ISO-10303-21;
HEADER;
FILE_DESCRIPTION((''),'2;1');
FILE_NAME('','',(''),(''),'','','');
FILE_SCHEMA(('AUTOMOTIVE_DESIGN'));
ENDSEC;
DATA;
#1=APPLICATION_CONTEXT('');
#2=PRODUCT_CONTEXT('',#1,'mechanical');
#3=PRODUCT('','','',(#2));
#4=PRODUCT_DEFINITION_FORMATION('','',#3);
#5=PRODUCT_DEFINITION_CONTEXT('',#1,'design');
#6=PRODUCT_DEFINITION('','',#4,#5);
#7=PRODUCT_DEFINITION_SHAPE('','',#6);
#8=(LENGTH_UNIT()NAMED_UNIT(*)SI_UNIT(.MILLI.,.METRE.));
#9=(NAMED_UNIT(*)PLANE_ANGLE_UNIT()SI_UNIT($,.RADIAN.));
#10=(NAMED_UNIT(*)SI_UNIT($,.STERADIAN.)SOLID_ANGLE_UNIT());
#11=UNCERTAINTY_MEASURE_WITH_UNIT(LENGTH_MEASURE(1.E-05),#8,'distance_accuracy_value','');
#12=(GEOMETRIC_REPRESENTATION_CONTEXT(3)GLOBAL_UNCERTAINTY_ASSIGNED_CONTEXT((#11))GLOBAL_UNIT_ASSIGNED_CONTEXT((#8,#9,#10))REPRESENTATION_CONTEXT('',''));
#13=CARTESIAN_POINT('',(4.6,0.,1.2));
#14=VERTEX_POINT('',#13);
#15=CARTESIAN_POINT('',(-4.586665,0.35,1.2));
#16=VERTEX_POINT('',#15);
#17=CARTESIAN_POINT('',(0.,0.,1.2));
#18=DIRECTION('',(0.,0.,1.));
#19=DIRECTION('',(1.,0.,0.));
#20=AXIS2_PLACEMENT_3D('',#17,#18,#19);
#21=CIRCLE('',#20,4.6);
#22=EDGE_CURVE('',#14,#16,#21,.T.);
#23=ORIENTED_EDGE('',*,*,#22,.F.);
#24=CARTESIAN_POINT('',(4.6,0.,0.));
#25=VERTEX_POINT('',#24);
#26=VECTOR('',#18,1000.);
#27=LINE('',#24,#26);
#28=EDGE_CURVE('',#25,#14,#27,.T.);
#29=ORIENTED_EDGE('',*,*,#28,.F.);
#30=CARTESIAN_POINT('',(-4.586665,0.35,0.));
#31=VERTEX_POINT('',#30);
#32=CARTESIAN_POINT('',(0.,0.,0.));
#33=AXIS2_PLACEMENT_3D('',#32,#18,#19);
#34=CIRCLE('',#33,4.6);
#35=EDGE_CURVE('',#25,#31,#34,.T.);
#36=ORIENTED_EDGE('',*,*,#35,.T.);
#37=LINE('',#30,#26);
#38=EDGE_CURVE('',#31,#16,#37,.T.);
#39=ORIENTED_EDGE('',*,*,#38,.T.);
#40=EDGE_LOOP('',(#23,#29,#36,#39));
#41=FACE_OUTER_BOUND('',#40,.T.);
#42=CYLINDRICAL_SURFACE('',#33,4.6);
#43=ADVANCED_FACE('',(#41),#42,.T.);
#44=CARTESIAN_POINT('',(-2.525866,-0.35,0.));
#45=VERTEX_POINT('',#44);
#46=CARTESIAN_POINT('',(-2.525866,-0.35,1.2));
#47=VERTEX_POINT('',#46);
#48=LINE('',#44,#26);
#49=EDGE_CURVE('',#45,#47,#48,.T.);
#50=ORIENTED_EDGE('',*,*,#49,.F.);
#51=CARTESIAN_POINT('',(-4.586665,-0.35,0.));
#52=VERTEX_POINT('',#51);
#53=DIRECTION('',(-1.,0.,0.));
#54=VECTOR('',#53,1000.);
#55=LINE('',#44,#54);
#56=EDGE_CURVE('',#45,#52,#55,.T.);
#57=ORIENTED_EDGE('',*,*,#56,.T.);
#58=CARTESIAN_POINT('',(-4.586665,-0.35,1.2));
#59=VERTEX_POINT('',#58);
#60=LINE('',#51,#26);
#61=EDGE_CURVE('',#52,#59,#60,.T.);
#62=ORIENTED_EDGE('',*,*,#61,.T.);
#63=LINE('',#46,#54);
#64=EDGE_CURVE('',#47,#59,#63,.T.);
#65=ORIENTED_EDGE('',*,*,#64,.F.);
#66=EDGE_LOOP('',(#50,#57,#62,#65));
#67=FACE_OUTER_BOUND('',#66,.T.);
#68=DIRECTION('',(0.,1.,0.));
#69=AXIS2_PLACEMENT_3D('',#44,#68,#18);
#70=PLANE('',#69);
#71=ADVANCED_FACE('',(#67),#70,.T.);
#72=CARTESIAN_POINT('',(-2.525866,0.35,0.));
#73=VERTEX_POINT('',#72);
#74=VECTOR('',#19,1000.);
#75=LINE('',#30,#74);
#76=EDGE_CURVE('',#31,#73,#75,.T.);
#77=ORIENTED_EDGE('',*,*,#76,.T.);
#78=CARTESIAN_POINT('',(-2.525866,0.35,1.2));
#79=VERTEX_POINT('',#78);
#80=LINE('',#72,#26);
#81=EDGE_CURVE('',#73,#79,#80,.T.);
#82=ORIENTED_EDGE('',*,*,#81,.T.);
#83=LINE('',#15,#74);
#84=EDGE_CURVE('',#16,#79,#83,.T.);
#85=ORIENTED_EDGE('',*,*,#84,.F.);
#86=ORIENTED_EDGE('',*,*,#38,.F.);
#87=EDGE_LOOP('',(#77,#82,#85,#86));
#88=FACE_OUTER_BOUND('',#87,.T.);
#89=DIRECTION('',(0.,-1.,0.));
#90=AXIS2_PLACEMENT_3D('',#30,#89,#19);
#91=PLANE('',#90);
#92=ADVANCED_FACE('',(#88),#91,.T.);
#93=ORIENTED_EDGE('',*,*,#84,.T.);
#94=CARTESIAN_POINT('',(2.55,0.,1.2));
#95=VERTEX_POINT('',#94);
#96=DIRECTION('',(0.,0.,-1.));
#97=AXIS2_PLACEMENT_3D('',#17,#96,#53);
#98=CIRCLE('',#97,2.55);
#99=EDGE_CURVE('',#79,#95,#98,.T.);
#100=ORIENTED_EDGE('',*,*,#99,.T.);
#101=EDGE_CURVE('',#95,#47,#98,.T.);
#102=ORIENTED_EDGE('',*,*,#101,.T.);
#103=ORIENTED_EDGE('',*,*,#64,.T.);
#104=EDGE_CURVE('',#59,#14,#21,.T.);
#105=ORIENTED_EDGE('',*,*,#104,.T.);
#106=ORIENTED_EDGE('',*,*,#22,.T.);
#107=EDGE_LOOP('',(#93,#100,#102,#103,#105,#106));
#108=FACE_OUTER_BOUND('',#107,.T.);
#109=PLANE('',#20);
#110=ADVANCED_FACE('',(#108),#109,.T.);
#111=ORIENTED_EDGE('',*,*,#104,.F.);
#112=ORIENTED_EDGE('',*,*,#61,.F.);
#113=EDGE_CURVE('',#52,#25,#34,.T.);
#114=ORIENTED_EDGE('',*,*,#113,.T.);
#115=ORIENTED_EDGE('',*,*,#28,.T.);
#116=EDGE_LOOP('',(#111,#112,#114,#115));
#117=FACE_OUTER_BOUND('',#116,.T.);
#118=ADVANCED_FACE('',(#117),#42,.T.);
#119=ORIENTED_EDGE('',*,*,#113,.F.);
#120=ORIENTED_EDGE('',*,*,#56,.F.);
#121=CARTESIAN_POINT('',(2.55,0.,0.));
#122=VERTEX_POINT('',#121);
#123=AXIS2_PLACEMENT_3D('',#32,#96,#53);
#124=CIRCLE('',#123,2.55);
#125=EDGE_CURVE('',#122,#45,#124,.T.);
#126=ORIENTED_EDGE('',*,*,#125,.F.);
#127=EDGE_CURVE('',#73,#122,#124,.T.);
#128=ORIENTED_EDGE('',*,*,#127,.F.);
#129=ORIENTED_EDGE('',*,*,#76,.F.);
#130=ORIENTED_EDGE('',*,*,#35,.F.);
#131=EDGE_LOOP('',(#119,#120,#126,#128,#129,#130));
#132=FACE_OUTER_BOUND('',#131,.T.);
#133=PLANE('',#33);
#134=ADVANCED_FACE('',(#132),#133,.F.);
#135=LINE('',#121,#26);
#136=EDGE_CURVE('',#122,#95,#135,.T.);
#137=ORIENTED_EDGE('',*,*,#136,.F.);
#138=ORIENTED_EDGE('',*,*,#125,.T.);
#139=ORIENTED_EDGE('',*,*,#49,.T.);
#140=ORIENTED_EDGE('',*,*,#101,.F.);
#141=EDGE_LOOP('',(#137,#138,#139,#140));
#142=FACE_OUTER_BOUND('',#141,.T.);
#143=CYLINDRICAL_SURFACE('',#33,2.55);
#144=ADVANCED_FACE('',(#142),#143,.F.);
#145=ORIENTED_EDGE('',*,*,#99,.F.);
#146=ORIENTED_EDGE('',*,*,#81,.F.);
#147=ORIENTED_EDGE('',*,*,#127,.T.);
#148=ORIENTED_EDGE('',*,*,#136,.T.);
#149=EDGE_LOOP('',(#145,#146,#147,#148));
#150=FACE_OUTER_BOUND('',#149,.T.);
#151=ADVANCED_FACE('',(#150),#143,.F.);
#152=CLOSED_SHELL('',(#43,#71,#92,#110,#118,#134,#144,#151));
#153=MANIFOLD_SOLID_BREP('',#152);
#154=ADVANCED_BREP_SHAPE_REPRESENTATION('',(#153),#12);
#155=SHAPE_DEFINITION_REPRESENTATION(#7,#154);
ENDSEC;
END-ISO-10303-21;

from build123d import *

# Parameters (mm, degrees)
EXTRUDE_1_DEPTH = 1.2


with BuildPart() as part:
    # 草图1 → 凸台-拉伸1 (new body)
    with BuildSketch(Plane.XY.offset(1.2)):
        with BuildLine():
            Line((-4.586665455, 0.35), (-2.525866188, 0.35))
            ThreePointArc((-2.525866188, 0.35), (2.55, 0), (-2.525866188, -0.35))
            Line((-2.525866188, -0.35), (-4.586665455, -0.35))
            ThreePointArc((-4.586665455, -0.35), (4.6, 0), (-4.586665455, 0.35))
        make_face()
    extrude(amount=-EXTRUDE_1_DEPTH)


solid = part.part
